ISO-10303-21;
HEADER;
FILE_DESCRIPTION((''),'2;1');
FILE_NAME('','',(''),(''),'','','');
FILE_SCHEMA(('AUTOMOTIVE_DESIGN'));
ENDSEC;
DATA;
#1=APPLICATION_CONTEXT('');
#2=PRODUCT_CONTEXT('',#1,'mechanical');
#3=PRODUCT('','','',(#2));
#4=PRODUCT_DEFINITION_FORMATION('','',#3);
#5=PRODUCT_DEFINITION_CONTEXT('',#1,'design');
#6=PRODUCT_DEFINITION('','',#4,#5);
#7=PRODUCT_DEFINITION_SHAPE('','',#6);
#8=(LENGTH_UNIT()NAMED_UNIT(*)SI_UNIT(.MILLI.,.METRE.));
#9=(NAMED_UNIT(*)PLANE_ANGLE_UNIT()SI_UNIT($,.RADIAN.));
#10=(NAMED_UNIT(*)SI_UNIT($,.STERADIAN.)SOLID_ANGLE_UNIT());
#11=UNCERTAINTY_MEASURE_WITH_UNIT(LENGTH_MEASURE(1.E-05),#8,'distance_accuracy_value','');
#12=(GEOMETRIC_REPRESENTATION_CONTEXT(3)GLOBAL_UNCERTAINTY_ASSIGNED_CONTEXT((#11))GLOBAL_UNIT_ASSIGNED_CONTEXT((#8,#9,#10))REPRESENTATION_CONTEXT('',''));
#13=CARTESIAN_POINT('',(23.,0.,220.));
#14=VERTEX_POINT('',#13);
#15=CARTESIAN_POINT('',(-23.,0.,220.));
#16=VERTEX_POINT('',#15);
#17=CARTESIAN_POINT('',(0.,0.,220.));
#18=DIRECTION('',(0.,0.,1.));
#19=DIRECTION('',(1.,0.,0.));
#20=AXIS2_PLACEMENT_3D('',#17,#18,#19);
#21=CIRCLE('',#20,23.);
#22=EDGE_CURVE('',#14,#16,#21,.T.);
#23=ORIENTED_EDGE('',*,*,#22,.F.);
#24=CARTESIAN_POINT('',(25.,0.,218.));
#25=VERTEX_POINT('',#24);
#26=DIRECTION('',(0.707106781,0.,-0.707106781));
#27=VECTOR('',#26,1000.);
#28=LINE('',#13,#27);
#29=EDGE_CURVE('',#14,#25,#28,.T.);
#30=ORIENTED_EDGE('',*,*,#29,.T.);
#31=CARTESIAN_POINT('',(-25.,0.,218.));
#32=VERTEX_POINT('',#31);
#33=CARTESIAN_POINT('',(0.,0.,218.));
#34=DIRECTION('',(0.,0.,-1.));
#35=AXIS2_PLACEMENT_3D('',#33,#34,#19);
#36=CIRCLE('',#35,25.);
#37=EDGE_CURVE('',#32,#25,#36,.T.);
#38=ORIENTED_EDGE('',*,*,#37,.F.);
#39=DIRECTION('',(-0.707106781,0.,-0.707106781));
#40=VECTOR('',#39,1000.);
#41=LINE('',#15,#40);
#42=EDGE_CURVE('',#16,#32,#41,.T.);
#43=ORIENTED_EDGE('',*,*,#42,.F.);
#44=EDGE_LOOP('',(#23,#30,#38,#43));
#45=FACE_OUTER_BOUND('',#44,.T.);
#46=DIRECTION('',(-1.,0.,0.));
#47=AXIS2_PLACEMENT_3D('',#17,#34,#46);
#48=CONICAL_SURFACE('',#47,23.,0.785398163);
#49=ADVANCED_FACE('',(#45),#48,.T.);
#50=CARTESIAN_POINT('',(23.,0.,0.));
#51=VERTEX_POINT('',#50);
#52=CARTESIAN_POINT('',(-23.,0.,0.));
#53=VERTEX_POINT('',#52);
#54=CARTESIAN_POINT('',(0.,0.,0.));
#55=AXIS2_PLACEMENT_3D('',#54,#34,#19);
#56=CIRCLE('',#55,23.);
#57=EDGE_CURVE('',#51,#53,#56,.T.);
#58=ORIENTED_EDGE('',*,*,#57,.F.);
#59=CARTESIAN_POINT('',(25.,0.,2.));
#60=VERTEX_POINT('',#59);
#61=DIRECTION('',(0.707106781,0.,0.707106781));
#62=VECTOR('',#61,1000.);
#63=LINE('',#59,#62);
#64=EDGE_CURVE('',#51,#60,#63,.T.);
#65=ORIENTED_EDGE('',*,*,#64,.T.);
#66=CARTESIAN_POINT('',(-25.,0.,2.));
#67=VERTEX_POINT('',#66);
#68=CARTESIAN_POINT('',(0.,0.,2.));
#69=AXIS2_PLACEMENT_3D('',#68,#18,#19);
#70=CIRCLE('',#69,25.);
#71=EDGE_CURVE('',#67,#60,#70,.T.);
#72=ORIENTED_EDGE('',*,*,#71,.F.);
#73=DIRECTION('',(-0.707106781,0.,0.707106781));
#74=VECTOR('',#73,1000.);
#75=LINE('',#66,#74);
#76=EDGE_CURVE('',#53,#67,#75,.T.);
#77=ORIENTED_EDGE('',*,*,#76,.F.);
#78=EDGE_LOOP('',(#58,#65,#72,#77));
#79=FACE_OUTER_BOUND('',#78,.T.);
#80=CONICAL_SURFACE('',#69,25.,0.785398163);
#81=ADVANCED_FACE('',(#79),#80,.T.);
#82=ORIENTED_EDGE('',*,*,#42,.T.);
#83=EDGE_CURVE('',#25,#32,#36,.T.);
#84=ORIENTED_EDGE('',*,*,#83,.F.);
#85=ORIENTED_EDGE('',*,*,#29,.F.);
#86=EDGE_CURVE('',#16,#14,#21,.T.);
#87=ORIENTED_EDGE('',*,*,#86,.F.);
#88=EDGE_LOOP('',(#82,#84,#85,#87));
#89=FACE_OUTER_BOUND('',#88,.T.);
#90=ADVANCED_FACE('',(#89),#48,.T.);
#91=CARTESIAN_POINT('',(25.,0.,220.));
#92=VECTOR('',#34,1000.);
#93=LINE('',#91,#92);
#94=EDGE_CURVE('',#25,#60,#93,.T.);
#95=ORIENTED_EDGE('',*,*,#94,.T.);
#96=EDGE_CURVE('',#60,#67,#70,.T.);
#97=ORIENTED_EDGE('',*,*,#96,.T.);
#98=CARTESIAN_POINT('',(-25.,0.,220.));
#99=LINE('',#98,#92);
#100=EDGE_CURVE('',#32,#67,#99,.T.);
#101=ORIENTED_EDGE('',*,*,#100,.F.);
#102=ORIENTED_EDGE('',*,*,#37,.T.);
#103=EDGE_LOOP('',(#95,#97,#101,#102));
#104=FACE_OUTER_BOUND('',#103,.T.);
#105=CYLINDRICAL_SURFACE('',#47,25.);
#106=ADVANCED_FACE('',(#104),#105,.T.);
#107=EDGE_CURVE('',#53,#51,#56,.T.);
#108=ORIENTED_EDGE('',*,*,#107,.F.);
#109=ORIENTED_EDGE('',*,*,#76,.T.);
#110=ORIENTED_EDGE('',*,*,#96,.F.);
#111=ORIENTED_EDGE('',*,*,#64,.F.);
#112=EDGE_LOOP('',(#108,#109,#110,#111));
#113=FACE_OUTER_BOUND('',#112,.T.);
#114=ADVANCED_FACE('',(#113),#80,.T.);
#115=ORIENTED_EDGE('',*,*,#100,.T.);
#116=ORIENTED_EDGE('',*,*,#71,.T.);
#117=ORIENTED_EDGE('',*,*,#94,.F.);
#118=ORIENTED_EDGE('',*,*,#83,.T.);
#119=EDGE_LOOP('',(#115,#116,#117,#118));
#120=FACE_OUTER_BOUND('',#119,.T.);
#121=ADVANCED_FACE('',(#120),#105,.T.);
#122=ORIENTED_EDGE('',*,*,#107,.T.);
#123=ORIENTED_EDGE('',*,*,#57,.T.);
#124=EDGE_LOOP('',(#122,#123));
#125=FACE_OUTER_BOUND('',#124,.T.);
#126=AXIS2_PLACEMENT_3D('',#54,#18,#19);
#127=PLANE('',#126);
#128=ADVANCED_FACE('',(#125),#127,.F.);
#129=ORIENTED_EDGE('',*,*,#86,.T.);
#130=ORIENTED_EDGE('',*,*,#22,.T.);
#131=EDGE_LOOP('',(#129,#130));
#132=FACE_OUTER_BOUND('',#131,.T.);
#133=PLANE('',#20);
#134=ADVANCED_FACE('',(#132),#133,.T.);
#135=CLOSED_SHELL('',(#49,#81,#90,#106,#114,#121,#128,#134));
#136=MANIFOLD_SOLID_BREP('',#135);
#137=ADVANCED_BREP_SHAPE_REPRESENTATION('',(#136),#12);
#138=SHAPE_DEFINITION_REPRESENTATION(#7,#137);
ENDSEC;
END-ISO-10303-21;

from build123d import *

# Parameters (mm, degrees)
SKETCH1_R           = 25
BOSS_EXTRUDE1_DEPTH = 220
CHAMFER1_SIZE       = 2


with BuildPart() as part:
    # Sketch1 → Boss-Extrude1 (new body)
    with BuildSketch(Plane.XY):
        Circle(SKETCH1_R)
    extrude(amount=BOSS_EXTRUDE1_DEPTH)

    # Chamfer1
    chamfer1_edges = [part.edges().sort_by_distance(p)[0] for p in [
        (-25, 0, 0),
        (-25, 0, 220),
    ]]
    chamfer(chamfer1_edges, length=CHAMFER1_SIZE)


solid = part.part
